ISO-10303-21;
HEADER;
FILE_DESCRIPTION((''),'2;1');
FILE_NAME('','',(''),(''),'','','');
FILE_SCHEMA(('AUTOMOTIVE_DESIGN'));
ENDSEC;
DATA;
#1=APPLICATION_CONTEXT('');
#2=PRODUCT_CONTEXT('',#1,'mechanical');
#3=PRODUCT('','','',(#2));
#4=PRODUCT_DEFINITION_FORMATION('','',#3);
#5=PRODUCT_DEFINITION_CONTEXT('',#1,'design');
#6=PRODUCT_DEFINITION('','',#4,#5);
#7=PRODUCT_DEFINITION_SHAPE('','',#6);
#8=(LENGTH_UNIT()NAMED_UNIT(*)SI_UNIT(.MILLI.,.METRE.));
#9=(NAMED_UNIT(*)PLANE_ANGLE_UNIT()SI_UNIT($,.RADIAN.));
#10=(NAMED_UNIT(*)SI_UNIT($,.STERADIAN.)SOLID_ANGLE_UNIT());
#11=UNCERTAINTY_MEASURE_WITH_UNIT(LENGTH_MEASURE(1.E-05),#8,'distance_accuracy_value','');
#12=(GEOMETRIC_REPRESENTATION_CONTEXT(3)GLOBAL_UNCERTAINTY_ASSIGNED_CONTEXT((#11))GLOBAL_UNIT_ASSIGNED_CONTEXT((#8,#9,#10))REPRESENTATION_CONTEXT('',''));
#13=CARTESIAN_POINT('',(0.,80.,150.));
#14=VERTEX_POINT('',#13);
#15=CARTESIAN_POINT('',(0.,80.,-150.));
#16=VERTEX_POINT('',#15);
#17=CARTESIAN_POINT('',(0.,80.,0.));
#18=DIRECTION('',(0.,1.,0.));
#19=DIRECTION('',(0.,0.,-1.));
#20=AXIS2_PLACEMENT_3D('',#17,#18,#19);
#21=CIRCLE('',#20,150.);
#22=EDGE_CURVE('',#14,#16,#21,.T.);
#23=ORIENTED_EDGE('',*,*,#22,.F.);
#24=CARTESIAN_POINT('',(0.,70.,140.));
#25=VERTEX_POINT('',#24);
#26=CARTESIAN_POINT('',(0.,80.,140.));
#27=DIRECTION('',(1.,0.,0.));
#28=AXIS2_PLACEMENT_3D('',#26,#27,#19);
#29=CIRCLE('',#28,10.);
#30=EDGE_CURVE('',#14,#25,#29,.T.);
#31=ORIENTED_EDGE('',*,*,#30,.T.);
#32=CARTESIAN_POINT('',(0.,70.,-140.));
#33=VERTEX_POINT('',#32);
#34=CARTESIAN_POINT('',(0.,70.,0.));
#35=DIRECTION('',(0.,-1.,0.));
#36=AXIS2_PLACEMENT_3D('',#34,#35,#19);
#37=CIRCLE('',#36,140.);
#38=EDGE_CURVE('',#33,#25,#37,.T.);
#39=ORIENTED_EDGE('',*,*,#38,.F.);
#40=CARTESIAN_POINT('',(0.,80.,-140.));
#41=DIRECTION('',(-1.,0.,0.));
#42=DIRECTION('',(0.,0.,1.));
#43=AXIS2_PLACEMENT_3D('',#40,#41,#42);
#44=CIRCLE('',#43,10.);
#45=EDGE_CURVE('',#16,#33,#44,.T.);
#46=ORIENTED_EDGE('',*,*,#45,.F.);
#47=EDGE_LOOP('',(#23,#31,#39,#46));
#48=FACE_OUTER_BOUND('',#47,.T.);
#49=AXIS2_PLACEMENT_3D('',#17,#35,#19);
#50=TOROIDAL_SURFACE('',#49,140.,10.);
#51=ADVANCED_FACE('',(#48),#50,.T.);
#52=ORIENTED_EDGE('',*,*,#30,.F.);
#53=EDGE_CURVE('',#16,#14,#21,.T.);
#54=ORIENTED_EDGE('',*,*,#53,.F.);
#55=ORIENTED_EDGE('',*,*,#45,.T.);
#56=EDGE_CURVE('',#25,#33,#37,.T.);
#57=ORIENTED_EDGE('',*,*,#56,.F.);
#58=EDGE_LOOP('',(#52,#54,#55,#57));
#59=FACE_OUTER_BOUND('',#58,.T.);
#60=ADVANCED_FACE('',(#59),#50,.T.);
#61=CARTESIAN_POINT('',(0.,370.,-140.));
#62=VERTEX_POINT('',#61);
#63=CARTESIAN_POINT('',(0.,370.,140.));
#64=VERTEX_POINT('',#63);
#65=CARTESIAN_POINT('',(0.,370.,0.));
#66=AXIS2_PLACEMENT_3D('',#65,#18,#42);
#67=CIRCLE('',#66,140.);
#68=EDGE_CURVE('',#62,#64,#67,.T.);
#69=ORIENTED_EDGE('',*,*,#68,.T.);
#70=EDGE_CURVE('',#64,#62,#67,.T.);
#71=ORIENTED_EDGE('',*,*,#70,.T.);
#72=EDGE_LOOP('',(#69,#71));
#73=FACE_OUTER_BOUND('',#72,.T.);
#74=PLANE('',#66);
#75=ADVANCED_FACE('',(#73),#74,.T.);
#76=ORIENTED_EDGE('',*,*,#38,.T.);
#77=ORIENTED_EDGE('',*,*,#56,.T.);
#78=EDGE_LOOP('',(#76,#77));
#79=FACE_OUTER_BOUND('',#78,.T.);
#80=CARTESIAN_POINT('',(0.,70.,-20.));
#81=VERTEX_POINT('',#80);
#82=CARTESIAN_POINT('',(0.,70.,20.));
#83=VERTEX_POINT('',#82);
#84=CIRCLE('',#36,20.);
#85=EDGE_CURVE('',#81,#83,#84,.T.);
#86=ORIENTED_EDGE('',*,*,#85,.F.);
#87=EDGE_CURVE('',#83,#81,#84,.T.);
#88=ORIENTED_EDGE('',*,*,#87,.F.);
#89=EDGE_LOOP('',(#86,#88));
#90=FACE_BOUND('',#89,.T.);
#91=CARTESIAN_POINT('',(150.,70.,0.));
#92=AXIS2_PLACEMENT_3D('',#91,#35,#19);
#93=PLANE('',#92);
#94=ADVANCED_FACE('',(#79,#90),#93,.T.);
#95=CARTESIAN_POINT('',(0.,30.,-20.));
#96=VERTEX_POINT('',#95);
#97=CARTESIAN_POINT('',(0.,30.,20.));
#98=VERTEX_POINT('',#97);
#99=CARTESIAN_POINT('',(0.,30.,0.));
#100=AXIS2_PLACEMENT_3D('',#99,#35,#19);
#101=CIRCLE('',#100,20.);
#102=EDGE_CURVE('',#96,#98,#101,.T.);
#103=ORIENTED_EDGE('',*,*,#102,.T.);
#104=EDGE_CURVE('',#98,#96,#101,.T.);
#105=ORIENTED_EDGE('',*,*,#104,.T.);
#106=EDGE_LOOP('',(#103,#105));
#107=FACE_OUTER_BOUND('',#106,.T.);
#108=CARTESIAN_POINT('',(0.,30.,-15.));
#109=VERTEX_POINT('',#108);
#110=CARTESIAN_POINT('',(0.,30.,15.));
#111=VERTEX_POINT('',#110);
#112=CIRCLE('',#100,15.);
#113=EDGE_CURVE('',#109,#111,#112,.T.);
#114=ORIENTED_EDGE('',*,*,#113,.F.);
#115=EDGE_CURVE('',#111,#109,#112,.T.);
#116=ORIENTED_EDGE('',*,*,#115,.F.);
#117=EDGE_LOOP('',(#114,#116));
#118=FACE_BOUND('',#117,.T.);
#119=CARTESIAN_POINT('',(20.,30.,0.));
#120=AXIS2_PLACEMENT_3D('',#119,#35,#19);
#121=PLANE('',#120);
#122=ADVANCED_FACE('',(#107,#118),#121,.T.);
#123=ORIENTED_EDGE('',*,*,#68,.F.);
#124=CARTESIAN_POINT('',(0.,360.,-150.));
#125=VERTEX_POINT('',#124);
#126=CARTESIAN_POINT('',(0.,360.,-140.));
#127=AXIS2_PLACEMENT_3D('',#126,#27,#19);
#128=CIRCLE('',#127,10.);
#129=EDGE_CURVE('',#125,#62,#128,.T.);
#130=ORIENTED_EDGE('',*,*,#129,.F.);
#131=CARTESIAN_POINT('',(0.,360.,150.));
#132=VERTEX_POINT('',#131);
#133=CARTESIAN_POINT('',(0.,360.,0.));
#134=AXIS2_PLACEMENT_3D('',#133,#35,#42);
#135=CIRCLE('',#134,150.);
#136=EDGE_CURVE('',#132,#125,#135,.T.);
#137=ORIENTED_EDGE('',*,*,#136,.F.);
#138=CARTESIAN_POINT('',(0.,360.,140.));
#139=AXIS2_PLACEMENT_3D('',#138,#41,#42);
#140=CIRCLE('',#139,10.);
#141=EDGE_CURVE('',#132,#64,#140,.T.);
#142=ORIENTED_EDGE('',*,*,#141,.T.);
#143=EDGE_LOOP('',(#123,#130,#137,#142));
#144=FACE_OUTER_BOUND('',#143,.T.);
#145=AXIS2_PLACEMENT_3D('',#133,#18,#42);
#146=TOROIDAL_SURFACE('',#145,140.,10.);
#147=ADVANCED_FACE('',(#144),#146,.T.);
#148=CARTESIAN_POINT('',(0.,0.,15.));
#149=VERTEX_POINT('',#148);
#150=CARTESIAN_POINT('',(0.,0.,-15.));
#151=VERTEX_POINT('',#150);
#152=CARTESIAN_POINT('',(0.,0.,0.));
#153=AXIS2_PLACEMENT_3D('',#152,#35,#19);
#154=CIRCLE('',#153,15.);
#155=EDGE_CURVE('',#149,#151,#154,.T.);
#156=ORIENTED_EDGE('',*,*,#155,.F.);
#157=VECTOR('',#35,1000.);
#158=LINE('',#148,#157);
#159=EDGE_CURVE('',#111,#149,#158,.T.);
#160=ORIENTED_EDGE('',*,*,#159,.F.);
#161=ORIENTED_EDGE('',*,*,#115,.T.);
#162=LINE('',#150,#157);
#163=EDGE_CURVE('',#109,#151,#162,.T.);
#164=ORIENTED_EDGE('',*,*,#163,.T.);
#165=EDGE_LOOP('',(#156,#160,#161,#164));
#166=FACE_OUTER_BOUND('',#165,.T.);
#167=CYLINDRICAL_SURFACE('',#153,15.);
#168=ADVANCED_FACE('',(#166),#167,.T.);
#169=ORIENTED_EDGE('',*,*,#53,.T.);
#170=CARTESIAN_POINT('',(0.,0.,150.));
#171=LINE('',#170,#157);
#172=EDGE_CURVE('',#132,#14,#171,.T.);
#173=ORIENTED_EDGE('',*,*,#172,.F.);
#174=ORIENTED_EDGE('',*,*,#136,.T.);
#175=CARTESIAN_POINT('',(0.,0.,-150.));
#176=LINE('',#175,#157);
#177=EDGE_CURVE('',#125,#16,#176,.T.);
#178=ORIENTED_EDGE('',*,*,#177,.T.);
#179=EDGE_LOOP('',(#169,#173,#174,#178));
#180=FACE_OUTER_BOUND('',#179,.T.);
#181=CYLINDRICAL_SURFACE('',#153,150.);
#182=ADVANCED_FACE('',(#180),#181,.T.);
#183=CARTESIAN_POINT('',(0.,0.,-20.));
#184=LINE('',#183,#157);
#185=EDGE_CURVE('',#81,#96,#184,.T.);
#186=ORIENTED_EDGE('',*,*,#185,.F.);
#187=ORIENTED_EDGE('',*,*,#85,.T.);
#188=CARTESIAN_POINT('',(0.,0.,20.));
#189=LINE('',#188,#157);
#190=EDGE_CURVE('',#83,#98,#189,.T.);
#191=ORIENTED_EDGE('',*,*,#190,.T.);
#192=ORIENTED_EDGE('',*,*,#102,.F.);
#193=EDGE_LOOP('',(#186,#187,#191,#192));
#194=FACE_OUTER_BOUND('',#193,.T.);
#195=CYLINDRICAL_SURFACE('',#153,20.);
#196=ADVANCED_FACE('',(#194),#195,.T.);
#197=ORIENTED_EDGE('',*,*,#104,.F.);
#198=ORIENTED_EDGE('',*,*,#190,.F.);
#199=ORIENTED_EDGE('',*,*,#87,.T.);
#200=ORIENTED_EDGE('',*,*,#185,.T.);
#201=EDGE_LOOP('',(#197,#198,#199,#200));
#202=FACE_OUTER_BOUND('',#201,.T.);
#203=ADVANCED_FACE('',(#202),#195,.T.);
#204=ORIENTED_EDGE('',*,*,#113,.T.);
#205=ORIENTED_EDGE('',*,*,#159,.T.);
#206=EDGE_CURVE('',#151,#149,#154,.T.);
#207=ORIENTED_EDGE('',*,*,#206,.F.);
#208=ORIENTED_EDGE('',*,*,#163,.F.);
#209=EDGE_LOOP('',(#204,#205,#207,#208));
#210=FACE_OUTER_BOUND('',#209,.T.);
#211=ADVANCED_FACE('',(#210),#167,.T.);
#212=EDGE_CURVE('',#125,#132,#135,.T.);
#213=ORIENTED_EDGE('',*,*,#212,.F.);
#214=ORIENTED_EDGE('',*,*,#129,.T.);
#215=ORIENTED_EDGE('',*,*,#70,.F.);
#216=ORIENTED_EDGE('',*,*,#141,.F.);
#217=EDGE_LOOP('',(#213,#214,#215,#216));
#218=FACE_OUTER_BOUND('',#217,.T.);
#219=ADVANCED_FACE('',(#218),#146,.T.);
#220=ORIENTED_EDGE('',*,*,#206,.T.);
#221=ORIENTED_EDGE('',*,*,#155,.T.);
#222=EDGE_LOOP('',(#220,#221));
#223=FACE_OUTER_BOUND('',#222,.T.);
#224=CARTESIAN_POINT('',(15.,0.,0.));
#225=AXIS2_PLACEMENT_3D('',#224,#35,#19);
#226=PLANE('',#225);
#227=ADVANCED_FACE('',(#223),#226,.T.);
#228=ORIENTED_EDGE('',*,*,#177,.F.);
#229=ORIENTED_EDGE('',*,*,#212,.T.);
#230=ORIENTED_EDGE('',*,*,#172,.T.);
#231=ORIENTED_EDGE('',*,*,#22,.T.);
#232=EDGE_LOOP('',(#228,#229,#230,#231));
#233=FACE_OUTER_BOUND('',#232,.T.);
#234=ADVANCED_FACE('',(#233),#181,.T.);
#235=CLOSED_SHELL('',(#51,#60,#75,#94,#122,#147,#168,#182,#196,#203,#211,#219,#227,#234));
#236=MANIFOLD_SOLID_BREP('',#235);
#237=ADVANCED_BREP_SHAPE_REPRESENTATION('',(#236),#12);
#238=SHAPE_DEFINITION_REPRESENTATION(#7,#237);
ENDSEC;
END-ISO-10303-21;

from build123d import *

# Parameters (mm, degrees)
FILLET1_R = 10


with BuildPart() as part:
    # Sketch1 → Revolve1 (revolve)
    with BuildSketch(Plane.XY, mode=Mode.PRIVATE) as revolve1_sk:
        Polygon((0, 0), (0, 370), (150, 370), (150, 70), (20, 70), (20, 30), (15, 30), (15, 0), align=None)
    revolve(revolve1_sk.sketch.rotate(Axis((0, 0, 0), (0, 1, 0)), 90), axis=Axis((0, 0, 0), (0, 1, 0)))

    # Fillet1
    fillet1_edges = [part.edges().sort_by_distance(p)[0] for p in [
        (0, 70, 150),
        (0, 370, 150),
    ]]
    fillet(fillet1_edges, radius=FILLET1_R)


solid = part.part
